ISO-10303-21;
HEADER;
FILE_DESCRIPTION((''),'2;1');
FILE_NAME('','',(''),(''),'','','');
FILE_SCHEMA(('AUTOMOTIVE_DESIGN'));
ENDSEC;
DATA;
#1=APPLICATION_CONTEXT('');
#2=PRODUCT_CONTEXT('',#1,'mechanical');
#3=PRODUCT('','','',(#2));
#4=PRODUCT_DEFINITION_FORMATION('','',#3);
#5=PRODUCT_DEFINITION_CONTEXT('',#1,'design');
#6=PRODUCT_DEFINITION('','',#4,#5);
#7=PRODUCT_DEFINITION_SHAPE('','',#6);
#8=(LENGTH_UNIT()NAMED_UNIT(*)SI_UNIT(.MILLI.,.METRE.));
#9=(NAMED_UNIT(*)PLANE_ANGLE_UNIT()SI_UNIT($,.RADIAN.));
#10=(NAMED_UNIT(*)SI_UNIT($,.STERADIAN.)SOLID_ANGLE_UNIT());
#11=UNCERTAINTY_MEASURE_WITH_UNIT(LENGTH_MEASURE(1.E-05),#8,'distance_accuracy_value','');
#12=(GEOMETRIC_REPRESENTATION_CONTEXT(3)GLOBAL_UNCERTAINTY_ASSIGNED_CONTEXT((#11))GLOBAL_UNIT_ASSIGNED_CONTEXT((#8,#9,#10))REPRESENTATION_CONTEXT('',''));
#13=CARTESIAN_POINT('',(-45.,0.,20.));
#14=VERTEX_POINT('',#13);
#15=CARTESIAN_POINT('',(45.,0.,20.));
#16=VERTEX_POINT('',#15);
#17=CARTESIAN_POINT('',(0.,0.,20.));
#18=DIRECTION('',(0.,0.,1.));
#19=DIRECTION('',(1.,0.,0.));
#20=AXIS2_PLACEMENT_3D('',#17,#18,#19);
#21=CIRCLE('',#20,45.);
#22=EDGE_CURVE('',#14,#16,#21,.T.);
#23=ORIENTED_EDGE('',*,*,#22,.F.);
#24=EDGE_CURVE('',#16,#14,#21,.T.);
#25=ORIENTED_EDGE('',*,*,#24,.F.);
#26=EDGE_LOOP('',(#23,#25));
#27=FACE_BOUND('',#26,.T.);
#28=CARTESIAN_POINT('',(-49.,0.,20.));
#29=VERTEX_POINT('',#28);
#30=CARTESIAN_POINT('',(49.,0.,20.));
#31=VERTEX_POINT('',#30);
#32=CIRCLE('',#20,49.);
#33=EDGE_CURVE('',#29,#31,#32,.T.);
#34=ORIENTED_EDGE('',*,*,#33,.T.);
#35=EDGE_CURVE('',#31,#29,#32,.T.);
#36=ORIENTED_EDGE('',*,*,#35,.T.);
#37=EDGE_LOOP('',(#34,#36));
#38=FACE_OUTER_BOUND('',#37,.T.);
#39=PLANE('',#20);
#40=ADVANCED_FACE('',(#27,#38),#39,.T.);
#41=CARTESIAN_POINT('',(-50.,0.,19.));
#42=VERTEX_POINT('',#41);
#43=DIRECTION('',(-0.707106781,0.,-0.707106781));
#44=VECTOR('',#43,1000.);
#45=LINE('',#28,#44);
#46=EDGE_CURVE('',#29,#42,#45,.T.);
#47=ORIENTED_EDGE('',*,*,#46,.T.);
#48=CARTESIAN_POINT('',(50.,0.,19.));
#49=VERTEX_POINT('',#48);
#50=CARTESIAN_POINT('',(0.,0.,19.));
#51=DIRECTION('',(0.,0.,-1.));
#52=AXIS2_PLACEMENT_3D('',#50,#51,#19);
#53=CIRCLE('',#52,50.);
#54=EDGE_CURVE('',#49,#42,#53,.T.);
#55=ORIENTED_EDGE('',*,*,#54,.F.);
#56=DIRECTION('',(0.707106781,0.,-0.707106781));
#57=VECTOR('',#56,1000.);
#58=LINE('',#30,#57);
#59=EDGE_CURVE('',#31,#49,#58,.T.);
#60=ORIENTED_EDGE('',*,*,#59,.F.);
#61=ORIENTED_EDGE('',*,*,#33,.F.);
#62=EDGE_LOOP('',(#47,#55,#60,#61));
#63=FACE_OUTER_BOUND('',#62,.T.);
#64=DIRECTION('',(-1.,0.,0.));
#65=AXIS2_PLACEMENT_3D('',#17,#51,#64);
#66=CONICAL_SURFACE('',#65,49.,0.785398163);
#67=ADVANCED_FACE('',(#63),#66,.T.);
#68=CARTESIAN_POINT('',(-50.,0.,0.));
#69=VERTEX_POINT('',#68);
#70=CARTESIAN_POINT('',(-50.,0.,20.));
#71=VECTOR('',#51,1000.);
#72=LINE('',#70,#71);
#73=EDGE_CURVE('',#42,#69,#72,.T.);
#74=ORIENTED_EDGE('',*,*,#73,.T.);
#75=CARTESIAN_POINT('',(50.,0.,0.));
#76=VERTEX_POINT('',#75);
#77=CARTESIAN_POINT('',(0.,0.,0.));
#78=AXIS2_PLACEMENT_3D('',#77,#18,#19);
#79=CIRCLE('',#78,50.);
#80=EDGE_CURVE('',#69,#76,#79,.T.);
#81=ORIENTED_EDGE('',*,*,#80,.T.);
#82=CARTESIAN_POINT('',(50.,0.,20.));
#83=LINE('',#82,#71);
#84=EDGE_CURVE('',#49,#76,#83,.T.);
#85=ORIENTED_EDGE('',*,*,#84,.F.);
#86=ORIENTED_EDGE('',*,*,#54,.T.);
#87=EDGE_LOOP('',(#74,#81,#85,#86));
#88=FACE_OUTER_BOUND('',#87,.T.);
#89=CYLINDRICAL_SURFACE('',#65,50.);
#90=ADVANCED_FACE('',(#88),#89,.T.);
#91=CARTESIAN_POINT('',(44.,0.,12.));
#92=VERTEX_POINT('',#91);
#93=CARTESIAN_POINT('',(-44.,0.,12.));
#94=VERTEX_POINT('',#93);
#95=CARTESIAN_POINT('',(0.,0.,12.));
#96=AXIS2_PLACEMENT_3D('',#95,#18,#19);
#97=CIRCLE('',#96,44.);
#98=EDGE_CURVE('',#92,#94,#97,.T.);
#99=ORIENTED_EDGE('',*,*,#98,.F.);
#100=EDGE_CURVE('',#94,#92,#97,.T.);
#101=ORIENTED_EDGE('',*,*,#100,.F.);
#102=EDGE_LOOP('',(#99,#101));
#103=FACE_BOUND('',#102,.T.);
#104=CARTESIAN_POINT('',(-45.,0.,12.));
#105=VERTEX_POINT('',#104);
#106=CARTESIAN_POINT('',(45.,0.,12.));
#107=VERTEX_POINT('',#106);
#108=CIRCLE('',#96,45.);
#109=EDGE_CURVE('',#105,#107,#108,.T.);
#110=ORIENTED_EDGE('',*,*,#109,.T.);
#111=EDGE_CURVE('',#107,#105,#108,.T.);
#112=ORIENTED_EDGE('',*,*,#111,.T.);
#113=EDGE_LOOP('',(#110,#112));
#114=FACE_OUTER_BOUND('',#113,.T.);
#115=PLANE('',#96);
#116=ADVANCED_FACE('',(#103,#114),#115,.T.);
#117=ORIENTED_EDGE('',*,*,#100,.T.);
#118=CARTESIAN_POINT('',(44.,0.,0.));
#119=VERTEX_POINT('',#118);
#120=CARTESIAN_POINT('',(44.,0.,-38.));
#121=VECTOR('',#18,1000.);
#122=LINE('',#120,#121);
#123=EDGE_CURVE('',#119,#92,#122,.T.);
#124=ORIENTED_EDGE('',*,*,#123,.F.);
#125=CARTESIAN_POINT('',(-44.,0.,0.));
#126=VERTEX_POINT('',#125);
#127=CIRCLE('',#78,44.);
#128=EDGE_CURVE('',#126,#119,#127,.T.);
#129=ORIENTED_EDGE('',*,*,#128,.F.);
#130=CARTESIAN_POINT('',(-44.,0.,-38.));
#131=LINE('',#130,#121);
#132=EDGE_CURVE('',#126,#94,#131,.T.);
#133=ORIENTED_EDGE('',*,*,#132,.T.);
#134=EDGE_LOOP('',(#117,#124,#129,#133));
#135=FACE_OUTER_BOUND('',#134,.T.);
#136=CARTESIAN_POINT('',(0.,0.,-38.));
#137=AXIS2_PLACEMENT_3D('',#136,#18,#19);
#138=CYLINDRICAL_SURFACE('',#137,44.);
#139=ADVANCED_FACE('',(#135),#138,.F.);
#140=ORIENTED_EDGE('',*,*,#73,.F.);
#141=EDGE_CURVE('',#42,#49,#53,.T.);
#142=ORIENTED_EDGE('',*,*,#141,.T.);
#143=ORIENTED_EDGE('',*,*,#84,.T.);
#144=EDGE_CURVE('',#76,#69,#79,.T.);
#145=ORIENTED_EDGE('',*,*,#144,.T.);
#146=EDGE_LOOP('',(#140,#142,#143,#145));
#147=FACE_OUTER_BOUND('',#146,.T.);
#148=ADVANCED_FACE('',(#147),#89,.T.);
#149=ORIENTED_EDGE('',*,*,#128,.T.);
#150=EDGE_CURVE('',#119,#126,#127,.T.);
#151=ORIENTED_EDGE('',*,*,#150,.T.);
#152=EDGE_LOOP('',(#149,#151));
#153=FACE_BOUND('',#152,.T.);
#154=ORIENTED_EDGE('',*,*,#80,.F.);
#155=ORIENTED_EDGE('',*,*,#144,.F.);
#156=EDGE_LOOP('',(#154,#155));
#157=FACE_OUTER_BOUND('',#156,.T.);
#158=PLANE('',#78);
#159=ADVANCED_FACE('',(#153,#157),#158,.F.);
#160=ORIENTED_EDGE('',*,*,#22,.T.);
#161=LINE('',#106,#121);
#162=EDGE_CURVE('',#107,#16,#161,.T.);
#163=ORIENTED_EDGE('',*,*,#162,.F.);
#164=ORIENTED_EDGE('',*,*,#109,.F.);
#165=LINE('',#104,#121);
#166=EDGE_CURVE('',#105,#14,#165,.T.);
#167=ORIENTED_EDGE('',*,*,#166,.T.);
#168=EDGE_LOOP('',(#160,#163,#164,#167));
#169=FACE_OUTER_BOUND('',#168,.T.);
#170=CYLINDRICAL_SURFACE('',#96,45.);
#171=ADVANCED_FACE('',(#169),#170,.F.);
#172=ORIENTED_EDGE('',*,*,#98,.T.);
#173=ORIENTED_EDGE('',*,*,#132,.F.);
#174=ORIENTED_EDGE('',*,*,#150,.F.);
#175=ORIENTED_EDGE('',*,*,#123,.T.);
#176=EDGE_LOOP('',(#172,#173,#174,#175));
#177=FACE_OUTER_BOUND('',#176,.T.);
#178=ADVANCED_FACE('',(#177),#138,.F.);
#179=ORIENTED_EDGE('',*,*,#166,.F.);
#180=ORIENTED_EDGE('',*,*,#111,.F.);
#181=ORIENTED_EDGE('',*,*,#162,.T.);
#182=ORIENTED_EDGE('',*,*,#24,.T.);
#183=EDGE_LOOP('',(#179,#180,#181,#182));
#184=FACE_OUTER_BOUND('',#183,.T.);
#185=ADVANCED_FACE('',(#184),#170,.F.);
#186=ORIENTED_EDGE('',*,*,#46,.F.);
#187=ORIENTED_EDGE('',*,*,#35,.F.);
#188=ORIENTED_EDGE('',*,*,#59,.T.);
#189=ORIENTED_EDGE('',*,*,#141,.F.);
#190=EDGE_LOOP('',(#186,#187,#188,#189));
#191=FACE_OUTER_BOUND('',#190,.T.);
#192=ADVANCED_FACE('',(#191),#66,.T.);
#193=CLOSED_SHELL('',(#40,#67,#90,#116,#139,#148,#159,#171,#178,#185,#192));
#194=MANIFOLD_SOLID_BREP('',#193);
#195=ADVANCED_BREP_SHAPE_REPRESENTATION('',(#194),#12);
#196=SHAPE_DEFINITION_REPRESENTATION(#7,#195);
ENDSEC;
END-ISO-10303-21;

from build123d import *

# Parameters (mm, degrees)
RIM_OD_SKETCH_100_R       = 50
RIM_BLANK_100X20_DEPTH    = 20
RECESS_SKETCH_90_R        = 45
RECESS_90X8_DEPTH         = 8
BORE_SKETCH_88_R          = 44
BORE_88_THROUGH_DEPTH     = 50
EDGE_CHAMFER_1X45DEG_SIZE = 1


with BuildPart() as part:
    # Rim OD Sketch Ø100 → Rim Blank Ø100x20 (new body)
    with BuildSketch(Plane.XY):
        Circle(RIM_OD_SKETCH_100_R)
    extrude(amount=RIM_BLANK_100X20_DEPTH)

    # Recess Sketch Ø90 → Recess Ø90x8 (cut)
    with BuildSketch(Plane.XY.offset(20)):
        Circle(RECESS_SKETCH_90_R)
    extrude(amount=-RECESS_90X8_DEPTH, mode=Mode.SUBTRACT)

    # Bore Sketch Ø88 → Bore Ø88 Through (cut)
    with BuildSketch(Plane.XY.offset(12)):
        Circle(BORE_SKETCH_88_R)
    extrude(amount=-BORE_88_THROUGH_DEPTH, mode=Mode.SUBTRACT)

    # Edge Chamfer 1x45deg
    edge_chamfer_1x45deg_edges = [part.edges().sort_by_distance(p)[0] for p in [
        (-50, 0, 20),
    ]]
    chamfer(edge_chamfer_1x45deg_edges, length=EDGE_CHAMFER_1X45DEG_SIZE)


solid = part.part
